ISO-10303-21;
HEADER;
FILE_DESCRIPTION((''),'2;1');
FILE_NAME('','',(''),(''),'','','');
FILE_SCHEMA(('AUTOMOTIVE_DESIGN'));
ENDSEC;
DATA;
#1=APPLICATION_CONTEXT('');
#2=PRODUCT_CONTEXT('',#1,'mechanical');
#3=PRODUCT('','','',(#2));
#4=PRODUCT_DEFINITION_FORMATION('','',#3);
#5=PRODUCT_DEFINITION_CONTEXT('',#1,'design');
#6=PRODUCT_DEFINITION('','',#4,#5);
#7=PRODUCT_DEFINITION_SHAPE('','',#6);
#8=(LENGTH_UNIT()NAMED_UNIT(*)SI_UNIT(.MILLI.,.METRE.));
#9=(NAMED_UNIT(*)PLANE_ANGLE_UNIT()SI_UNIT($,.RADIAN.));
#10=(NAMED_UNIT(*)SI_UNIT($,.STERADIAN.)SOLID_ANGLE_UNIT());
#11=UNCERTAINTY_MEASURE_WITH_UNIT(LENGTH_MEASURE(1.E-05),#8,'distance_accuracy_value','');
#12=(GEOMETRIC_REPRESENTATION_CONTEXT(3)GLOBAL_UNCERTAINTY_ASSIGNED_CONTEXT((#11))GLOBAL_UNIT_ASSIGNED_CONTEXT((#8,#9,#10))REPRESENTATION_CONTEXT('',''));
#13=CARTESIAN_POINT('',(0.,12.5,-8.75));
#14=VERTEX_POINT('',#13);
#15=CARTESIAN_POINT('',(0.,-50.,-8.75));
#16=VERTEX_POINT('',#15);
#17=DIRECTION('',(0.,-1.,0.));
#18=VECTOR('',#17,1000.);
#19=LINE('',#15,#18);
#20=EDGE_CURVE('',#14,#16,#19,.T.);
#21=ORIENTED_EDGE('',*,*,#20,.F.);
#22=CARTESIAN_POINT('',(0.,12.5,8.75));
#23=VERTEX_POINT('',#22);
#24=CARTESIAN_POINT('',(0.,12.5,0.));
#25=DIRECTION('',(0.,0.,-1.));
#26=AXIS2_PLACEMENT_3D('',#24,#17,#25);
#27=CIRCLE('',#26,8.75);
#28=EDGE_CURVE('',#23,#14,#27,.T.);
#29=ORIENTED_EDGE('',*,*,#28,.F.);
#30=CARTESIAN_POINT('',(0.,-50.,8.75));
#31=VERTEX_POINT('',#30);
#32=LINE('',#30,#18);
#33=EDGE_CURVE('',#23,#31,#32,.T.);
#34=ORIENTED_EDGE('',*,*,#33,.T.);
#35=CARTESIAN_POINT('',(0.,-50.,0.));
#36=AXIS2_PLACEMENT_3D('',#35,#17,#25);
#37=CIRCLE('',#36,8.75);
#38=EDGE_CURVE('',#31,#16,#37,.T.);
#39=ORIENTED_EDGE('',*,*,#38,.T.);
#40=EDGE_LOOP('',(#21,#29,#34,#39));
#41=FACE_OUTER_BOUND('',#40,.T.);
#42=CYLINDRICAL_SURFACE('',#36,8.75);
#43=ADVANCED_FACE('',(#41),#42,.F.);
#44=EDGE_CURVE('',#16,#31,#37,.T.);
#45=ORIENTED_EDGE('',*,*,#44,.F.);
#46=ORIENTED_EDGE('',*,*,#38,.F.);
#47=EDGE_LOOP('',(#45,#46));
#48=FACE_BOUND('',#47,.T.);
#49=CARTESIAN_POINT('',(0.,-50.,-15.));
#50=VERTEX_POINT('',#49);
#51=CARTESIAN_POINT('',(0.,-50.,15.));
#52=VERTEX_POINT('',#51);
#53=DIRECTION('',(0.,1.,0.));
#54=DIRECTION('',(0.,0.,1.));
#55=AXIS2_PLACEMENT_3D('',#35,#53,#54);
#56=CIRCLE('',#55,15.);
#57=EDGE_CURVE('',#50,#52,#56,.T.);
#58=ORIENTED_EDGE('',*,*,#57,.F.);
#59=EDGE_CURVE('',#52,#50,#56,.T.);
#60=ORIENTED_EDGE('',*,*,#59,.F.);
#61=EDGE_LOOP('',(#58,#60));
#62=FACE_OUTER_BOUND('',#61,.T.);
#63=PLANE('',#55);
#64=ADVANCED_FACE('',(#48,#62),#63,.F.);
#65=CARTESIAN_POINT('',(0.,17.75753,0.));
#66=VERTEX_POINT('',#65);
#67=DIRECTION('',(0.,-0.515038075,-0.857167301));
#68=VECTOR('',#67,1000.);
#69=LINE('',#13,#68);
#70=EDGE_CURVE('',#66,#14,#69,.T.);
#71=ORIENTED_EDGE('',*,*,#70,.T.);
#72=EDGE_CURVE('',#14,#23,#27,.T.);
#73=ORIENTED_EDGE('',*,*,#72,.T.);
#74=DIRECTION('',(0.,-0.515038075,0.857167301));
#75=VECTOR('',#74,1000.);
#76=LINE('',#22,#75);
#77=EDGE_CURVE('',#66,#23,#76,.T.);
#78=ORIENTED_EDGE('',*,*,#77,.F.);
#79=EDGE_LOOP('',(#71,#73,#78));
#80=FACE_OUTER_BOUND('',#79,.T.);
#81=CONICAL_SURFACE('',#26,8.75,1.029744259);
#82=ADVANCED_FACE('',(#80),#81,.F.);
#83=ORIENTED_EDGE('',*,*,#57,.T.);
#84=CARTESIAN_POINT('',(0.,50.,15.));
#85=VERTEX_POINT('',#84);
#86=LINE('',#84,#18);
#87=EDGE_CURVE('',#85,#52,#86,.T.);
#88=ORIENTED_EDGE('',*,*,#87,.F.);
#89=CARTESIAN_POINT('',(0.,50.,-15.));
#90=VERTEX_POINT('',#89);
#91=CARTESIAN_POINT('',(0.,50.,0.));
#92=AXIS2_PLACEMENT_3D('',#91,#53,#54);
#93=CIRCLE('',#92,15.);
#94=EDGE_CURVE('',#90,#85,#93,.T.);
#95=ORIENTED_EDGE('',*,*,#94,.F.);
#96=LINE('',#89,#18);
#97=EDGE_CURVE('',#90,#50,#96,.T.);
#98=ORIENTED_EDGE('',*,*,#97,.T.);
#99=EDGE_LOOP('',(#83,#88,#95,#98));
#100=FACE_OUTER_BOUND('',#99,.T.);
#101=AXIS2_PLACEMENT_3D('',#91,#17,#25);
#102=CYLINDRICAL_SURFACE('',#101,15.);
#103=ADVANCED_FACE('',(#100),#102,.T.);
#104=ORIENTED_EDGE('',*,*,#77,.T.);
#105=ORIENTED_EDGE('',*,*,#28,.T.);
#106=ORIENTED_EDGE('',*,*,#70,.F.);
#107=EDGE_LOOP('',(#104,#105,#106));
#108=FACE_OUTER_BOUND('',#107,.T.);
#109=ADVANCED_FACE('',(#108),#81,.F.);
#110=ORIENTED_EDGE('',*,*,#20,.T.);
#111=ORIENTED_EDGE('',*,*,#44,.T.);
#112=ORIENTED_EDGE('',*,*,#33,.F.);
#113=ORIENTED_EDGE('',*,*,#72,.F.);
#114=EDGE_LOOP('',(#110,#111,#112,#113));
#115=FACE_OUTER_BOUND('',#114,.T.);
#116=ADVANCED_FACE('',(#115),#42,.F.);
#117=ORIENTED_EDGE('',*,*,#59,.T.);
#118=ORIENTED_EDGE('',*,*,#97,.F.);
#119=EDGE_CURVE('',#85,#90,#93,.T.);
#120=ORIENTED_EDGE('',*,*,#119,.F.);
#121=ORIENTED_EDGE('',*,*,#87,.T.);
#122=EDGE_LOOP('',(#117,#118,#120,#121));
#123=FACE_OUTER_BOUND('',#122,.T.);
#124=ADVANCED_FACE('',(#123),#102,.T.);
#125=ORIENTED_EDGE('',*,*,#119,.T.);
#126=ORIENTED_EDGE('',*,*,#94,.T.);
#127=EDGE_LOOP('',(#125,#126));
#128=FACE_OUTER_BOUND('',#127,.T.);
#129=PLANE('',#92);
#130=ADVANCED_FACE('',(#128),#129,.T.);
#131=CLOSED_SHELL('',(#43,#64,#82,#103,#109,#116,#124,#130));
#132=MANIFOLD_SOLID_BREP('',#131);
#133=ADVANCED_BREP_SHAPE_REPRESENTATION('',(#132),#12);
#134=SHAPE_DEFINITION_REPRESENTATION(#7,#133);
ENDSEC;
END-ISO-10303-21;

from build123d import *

# Parameters (mm, degrees)
SKETCH1_R              = 15
BOSS_EXTRUDE1_DEPTH    = 50
M20_TAPPED_HOLE1_D     = 17.5
M20_TAPPED_HOLE1_DEPTH = 62.5
M20_TAPPED_HOLE1_TIP   = 5.257530416


with BuildPart() as part:
    # Sketch1 → Boss-Extrude1 (new, symmetric)
    with BuildSketch(Plane(origin=(0, 0, 0), x_dir=(1, 0, 0), z_dir=(0, 1, 0))):
        with Locations(Location((0, 0, 0), (0, 0, 270))):
            Circle(SKETCH1_R)
    extrude(amount=BOSS_EXTRUDE1_DEPTH, both=True)

    # M20 Tapped Hole1
    with Locations(Plane(origin=(0, -50, 0), x_dir=(0, 0, -1), z_dir=(0, -1, 0))):
        with Locations((0, 0)):
            Hole(M20_TAPPED_HOLE1_D / 2, depth=M20_TAPPED_HOLE1_DEPTH)
            with Locations((0, 0, -(M20_TAPPED_HOLE1_DEPTH + M20_TAPPED_HOLE1_TIP / 2))):  # 118° drill point
                Cone(0, M20_TAPPED_HOLE1_D / 2, M20_TAPPED_HOLE1_TIP, mode=Mode.SUBTRACT)


solid = part.part
